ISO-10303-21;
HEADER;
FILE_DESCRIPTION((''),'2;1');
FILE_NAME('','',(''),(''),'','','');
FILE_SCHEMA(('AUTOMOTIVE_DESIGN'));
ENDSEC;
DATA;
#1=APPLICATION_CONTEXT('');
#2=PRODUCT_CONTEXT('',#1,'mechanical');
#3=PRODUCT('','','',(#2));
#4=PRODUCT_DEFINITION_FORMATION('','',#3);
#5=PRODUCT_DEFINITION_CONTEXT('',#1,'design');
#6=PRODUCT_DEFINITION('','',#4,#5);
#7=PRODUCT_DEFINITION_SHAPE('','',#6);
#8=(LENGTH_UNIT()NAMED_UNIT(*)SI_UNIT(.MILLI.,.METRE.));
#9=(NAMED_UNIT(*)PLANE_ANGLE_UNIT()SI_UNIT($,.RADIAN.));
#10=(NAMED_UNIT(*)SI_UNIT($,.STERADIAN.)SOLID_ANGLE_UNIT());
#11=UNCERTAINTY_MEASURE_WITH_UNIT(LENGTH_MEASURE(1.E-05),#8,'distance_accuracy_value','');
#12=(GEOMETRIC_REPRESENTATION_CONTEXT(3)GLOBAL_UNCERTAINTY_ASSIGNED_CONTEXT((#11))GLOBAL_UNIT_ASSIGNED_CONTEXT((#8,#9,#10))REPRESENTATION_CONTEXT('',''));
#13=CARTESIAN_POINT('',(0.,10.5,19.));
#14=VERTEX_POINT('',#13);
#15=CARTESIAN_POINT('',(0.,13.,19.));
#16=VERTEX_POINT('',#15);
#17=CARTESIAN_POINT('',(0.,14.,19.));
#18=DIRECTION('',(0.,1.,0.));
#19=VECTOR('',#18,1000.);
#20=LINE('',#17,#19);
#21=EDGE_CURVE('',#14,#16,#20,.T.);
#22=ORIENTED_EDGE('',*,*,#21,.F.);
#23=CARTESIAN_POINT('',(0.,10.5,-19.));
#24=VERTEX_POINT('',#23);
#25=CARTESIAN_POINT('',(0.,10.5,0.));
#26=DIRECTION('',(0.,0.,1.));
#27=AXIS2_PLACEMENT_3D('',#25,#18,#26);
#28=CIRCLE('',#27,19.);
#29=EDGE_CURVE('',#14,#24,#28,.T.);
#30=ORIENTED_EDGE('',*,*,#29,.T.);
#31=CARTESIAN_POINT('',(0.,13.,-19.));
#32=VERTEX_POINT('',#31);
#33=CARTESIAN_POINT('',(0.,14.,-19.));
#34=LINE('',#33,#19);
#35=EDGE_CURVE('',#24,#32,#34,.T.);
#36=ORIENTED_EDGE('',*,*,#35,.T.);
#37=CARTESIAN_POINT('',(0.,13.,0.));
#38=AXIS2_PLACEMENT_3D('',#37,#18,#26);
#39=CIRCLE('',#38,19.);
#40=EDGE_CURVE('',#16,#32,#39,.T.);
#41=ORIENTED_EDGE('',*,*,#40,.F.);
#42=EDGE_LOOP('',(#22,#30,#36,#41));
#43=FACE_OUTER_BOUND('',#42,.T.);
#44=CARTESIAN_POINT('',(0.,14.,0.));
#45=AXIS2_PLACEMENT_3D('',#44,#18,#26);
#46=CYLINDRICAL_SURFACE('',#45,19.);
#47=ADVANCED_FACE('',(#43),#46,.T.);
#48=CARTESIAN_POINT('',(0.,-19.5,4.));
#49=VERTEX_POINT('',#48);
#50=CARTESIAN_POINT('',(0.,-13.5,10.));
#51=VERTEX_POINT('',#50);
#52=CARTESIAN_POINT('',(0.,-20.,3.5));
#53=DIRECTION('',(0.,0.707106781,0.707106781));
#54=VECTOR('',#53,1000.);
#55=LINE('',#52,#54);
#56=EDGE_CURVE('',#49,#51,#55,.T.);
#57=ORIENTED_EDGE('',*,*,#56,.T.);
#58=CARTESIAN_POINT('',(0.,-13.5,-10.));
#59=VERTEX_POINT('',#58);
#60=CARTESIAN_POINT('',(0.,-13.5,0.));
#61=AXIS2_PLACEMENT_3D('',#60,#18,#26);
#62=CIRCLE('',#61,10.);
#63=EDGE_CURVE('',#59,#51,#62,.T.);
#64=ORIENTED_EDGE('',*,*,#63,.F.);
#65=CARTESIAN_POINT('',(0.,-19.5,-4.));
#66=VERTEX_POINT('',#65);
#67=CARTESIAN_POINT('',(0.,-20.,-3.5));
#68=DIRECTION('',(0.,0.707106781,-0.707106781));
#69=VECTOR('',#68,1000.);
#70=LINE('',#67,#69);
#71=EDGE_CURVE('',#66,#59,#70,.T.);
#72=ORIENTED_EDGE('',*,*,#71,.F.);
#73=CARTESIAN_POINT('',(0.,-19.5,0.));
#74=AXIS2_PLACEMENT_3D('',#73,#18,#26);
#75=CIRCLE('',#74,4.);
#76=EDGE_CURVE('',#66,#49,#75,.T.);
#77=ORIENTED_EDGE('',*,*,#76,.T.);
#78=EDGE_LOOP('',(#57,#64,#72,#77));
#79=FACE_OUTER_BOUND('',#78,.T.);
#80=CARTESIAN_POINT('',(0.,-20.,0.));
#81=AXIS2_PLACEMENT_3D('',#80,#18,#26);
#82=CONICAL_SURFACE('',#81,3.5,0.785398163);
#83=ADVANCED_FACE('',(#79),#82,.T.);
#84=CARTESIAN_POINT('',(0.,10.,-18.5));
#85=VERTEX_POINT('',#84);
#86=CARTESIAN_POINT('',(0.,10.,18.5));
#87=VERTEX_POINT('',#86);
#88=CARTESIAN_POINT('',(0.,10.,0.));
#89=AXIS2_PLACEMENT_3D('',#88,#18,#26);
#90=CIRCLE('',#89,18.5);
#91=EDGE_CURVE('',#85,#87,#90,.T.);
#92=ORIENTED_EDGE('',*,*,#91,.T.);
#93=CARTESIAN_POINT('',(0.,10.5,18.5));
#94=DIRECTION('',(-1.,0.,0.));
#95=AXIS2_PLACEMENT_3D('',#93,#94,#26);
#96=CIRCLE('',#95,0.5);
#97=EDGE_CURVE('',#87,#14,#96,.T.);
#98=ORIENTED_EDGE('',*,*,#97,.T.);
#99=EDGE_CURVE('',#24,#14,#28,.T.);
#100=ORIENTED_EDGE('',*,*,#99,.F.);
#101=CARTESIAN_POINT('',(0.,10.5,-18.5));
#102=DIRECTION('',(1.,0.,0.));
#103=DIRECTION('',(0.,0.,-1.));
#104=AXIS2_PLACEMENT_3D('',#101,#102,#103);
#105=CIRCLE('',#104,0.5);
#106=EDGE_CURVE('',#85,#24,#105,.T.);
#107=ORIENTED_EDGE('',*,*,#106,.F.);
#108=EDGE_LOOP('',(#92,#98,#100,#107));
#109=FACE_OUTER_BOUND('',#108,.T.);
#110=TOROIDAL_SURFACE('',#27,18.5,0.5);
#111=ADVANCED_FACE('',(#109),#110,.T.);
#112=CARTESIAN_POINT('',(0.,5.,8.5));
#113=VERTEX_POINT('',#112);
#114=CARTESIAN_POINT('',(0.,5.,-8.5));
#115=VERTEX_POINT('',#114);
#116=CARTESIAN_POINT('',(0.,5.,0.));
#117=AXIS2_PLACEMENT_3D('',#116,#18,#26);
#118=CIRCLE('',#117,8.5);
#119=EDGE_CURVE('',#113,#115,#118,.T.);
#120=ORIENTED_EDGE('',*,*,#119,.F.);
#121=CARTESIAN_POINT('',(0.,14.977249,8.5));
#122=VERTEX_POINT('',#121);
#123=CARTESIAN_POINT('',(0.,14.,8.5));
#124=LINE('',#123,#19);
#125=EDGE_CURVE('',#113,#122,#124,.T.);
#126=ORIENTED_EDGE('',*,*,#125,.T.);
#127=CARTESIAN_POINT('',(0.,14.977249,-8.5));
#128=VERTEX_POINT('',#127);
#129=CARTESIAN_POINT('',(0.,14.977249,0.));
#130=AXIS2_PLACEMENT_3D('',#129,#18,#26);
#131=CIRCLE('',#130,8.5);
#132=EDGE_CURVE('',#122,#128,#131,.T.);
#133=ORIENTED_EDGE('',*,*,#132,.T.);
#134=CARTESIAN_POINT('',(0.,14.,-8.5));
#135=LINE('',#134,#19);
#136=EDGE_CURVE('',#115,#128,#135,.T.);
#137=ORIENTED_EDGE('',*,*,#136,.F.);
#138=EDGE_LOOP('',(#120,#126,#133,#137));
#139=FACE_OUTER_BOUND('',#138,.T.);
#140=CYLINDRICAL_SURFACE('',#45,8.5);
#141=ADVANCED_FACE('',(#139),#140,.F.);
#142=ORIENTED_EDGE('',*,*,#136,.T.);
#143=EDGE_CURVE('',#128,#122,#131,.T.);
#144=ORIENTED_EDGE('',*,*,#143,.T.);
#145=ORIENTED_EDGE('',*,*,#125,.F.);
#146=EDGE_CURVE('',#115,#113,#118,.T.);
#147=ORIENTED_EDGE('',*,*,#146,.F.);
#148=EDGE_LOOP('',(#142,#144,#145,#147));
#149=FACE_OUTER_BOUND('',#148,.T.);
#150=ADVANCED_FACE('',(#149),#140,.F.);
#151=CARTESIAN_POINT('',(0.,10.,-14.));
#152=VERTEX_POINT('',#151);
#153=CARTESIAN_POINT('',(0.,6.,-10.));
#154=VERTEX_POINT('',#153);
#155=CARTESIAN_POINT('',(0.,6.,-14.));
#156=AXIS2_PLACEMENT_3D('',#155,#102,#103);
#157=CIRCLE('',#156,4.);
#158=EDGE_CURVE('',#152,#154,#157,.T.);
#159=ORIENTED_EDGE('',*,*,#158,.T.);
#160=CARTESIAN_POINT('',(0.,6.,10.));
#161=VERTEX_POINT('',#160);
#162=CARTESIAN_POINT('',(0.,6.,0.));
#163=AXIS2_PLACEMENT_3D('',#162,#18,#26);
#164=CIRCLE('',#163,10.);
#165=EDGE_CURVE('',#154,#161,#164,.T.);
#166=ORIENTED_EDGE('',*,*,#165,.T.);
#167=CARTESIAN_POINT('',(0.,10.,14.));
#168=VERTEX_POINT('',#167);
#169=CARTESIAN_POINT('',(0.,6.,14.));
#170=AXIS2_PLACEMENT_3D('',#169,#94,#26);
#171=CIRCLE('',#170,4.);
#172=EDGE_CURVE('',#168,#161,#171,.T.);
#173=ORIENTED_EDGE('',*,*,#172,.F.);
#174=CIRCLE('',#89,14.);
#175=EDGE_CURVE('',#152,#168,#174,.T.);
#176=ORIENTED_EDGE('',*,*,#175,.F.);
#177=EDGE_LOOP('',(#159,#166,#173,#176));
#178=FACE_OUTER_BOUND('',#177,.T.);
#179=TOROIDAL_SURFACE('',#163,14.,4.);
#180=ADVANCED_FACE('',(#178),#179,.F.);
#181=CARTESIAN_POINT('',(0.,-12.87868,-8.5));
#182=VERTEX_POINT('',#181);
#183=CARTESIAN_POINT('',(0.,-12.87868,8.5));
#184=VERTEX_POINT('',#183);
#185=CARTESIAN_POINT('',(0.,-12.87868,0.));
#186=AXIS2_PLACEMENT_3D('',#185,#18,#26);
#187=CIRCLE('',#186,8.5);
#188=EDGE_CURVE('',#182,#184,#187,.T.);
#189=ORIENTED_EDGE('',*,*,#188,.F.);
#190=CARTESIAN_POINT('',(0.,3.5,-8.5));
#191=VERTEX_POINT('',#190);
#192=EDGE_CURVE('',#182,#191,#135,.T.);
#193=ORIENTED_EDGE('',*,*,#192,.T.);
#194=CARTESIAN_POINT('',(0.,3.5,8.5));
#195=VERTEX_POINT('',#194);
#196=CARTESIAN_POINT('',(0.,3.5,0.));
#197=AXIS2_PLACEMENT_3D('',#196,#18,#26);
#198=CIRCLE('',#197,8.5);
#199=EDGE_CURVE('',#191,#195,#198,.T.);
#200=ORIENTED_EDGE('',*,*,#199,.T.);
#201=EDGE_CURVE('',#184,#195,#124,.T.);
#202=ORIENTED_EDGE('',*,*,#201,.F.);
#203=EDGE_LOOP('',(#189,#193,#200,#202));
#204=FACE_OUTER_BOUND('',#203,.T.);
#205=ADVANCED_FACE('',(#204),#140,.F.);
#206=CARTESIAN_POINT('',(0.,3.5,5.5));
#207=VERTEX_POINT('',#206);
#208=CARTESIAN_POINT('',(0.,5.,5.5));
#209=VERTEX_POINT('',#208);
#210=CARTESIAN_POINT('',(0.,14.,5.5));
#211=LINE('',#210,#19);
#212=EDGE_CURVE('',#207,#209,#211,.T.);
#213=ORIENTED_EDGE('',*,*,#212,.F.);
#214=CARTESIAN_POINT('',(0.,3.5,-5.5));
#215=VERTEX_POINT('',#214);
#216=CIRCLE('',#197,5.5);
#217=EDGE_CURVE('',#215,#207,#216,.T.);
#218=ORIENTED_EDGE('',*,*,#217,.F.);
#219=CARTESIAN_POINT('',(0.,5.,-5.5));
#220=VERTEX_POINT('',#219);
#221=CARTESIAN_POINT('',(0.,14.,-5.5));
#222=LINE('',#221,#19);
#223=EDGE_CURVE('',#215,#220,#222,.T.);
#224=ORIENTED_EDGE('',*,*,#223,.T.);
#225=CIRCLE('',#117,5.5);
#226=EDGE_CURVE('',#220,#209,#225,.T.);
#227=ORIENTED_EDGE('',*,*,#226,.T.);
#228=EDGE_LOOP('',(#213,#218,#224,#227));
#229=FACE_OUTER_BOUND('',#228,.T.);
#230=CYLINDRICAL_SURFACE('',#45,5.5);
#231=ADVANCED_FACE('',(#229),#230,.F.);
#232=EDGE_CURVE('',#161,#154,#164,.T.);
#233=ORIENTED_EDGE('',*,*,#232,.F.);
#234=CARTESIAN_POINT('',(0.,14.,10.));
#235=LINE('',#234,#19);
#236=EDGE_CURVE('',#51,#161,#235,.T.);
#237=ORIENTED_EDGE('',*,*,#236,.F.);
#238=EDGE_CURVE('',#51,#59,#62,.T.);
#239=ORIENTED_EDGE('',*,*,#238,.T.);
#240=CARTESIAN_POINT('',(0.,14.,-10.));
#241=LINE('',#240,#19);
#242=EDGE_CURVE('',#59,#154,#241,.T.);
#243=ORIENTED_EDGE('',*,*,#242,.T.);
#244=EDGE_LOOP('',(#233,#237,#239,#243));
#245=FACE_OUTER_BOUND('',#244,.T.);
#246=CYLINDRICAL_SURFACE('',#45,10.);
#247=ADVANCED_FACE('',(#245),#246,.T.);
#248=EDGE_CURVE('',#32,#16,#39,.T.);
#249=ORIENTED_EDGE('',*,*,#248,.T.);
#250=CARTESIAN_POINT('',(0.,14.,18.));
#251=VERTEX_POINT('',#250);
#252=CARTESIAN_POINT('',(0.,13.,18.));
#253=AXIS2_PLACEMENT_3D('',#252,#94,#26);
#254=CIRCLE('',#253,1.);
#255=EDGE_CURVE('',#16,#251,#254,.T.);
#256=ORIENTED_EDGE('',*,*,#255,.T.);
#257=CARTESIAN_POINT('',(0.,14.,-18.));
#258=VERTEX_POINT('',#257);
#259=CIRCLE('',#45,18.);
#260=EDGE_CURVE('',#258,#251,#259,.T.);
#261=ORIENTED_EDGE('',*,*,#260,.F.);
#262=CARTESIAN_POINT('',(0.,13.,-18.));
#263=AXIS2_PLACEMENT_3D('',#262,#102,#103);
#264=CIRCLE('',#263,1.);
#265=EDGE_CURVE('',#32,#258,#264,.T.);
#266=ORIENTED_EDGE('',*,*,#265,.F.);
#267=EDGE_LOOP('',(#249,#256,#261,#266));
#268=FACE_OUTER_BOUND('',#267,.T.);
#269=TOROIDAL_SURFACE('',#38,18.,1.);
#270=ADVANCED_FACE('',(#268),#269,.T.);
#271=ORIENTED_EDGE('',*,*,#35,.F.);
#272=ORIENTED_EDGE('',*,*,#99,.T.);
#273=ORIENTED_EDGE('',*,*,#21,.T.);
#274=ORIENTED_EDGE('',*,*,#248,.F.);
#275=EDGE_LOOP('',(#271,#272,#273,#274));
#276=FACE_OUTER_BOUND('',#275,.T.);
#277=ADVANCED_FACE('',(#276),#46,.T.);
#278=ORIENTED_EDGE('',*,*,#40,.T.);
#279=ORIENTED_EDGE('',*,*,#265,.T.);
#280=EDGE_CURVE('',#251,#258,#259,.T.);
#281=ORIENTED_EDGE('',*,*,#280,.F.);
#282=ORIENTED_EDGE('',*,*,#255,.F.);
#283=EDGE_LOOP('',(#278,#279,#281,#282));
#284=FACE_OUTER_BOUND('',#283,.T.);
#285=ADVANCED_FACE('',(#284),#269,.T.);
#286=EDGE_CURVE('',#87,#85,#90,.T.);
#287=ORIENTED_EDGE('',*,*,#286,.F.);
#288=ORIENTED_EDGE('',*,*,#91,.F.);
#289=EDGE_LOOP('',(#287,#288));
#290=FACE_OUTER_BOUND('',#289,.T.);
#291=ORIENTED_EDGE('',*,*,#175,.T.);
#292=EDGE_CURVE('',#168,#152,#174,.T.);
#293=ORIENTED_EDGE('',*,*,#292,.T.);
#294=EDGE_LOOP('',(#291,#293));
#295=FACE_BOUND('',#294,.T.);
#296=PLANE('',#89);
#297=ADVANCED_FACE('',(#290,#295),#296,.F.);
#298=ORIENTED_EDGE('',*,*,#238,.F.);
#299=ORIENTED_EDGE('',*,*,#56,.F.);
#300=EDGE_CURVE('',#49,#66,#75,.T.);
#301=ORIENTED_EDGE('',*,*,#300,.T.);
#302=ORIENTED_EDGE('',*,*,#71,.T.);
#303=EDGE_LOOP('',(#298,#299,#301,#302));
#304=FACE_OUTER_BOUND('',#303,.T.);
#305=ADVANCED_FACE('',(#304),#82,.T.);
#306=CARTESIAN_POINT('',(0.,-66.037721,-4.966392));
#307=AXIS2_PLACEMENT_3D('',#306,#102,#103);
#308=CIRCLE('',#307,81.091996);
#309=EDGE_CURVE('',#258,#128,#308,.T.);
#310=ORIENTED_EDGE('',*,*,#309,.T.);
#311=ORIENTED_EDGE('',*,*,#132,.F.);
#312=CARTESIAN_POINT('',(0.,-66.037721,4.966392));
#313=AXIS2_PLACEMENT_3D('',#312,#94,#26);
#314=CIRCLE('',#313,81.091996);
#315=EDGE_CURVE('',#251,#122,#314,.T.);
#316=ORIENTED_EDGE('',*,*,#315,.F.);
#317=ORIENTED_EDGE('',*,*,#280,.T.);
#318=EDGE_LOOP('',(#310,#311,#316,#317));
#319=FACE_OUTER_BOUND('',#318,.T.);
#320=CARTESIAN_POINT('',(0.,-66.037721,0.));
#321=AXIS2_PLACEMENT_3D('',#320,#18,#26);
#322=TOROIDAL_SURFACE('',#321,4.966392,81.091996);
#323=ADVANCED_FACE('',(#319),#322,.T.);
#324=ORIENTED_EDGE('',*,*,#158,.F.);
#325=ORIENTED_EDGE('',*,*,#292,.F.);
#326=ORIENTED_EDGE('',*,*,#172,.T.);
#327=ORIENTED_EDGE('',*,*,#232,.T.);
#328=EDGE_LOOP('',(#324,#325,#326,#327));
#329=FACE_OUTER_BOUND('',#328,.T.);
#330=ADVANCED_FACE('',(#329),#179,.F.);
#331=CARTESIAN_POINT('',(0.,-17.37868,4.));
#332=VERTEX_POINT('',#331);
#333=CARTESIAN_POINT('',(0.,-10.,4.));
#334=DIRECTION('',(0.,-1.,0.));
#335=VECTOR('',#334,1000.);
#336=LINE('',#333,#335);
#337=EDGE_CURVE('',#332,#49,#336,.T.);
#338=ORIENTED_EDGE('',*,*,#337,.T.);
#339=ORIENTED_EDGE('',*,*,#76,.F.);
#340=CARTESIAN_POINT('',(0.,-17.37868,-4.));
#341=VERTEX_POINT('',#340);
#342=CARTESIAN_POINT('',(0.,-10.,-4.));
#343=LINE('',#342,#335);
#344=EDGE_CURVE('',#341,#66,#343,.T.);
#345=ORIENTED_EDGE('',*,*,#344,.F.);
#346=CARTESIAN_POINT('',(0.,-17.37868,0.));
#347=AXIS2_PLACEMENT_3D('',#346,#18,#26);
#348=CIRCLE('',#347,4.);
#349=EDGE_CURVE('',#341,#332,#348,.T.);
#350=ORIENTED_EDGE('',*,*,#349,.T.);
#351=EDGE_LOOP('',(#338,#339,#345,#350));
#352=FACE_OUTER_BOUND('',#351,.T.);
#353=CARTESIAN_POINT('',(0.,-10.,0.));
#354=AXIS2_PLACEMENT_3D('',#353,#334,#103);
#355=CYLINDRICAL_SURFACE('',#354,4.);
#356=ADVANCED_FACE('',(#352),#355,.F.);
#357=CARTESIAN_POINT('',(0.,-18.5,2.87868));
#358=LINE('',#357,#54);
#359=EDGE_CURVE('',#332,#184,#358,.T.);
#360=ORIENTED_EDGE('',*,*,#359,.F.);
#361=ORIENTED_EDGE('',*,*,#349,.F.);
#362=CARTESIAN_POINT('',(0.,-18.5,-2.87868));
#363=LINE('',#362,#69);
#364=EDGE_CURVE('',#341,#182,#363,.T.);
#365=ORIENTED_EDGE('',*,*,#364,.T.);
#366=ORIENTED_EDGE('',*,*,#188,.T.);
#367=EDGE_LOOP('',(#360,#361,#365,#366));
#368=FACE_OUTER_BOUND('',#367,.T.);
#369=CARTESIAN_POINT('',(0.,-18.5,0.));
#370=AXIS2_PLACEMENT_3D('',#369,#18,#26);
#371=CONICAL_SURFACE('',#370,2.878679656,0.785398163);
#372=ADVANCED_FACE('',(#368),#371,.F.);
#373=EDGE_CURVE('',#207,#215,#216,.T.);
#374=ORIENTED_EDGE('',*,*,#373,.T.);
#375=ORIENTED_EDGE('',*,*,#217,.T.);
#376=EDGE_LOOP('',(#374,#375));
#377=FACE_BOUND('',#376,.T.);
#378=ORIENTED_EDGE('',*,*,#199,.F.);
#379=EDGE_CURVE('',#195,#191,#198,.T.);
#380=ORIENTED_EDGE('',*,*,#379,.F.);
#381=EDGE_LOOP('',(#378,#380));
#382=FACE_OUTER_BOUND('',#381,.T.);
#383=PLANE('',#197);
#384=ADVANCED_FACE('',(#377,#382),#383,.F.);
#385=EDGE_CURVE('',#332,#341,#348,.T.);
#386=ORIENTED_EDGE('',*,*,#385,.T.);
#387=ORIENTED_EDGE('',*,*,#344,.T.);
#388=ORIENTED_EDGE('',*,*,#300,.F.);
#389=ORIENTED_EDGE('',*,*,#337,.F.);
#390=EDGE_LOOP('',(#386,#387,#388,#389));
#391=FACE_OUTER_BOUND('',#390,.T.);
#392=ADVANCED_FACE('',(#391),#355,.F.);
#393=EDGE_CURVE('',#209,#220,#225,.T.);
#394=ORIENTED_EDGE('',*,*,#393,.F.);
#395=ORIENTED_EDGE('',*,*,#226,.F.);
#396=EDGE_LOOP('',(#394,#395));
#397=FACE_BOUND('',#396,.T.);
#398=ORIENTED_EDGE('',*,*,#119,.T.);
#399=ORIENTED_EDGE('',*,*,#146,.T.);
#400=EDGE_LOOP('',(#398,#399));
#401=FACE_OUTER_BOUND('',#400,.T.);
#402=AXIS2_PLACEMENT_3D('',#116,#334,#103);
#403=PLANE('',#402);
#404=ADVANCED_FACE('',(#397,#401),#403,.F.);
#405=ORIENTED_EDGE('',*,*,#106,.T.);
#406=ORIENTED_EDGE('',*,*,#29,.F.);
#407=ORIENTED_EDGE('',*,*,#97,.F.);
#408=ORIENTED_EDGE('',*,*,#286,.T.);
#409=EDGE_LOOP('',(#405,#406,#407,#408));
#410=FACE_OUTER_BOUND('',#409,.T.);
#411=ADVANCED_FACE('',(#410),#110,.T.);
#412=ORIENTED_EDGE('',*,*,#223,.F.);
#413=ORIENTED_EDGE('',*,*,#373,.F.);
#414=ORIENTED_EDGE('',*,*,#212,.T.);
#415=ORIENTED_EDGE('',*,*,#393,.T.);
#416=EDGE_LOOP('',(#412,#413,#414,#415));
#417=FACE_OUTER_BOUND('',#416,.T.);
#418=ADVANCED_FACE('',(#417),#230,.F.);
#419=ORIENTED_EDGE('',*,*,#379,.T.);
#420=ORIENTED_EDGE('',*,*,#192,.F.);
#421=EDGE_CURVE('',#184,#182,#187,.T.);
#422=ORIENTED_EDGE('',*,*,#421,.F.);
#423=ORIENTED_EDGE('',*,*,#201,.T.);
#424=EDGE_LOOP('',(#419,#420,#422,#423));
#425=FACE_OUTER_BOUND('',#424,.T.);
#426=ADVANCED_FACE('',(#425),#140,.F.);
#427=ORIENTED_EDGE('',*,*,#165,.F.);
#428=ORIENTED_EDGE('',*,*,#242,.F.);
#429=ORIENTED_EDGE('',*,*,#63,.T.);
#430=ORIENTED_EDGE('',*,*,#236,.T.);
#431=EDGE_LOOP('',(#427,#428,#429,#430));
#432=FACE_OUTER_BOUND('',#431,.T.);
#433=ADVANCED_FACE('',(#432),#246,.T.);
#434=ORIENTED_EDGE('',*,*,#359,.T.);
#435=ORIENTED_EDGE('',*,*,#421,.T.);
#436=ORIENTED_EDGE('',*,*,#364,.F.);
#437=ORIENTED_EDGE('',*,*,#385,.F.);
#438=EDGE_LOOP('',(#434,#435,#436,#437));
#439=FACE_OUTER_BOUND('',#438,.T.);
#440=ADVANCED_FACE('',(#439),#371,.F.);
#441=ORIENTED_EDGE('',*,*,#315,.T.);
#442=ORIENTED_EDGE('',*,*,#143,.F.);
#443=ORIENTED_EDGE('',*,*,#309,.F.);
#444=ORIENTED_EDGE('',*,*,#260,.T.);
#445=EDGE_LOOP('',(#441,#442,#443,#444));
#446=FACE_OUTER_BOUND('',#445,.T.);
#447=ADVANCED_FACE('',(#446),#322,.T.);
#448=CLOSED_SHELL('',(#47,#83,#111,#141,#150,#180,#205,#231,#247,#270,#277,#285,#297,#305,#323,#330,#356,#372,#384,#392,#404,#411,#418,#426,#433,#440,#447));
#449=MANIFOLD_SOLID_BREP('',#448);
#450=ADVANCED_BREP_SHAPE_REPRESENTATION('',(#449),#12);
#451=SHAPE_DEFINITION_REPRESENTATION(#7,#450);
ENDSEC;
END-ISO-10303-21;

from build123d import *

# Parameters (mm, degrees)
SKETCH3_R          = 2.75
CUT_EXTRUDE1_DEPTH = 10
SKETCH4_R          = 4
CUT_EXTRUDE2_DEPTH = 10


with BuildPart() as part:
    # Sketch1 → Revolve1 (revolve)
    with BuildSketch(Plane.XY, mode=Mode.PRIVATE) as revolve1_sk:
        with BuildLine():
            Line((0, -20), (0, -18.5))
            Line((0, -18.5), (-2.878679656, -18.5))
            Line((-2.878679656, -18.5), (-8.5, -12.878679656))
            Line((-8.5, -12.878679656), (-8.5, 3.5))
            Line((-8.5, 3.5), (-5.5, 3.5))
            Line((-5.5, 3.5), (-5.5, 5))
            Line((-5.5, 5), (-8.5, 5))
            Line((-8.5, 5), (-8.5, 14.977248766))
            ThreePointArc((-8.5, 14.977248766), (-13.264398706, 14.628596634), (-18, 14))
            ThreePointArc((-18, 14), (-18.707106781, 13.707106781), (-19, 13))
            Line((-19, 13), (-19, 10.5))
            ThreePointArc((-19, 10.5), (-18.853553391, 10.146446609), (-18.5, 10))
            Line((-18.5, 10), (-14, 10))
            ThreePointArc((-14, 10), (-11.171572875, 8.828427125), (-10, 6))
            Line((-10, 6), (-10, -13.5))
            Line((-10, -13.5), (-3.5, -20))
            Line((-3.5, -20), (0, -20))
        make_face()
    revolve(revolve1_sk.sketch.rotate(Axis((0, 14, 0), (0, -1, 0)), 270), axis=Axis((0, 14, 0), (0, -1, 0)))

    # Sketch3 → Cut-Extrude1 (cut)
    with BuildSketch(Plane.XZ.offset(20)):
        with Locations(Location((0, 0, 0), (0, 0, 270))):
            Circle(SKETCH3_R)
    extrude(amount=-CUT_EXTRUDE1_DEPTH, mode=Mode.SUBTRACT)

    # Sketch4 → Cut-Extrude2 (cut)
    with BuildSketch(Plane.XZ.offset(20)):
        with Locations(Location((0, 0, 0), (0, 0, 90))):
            Circle(SKETCH4_R)
    extrude(amount=-CUT_EXTRUDE2_DEPTH, mode=Mode.SUBTRACT)


solid = part.part
